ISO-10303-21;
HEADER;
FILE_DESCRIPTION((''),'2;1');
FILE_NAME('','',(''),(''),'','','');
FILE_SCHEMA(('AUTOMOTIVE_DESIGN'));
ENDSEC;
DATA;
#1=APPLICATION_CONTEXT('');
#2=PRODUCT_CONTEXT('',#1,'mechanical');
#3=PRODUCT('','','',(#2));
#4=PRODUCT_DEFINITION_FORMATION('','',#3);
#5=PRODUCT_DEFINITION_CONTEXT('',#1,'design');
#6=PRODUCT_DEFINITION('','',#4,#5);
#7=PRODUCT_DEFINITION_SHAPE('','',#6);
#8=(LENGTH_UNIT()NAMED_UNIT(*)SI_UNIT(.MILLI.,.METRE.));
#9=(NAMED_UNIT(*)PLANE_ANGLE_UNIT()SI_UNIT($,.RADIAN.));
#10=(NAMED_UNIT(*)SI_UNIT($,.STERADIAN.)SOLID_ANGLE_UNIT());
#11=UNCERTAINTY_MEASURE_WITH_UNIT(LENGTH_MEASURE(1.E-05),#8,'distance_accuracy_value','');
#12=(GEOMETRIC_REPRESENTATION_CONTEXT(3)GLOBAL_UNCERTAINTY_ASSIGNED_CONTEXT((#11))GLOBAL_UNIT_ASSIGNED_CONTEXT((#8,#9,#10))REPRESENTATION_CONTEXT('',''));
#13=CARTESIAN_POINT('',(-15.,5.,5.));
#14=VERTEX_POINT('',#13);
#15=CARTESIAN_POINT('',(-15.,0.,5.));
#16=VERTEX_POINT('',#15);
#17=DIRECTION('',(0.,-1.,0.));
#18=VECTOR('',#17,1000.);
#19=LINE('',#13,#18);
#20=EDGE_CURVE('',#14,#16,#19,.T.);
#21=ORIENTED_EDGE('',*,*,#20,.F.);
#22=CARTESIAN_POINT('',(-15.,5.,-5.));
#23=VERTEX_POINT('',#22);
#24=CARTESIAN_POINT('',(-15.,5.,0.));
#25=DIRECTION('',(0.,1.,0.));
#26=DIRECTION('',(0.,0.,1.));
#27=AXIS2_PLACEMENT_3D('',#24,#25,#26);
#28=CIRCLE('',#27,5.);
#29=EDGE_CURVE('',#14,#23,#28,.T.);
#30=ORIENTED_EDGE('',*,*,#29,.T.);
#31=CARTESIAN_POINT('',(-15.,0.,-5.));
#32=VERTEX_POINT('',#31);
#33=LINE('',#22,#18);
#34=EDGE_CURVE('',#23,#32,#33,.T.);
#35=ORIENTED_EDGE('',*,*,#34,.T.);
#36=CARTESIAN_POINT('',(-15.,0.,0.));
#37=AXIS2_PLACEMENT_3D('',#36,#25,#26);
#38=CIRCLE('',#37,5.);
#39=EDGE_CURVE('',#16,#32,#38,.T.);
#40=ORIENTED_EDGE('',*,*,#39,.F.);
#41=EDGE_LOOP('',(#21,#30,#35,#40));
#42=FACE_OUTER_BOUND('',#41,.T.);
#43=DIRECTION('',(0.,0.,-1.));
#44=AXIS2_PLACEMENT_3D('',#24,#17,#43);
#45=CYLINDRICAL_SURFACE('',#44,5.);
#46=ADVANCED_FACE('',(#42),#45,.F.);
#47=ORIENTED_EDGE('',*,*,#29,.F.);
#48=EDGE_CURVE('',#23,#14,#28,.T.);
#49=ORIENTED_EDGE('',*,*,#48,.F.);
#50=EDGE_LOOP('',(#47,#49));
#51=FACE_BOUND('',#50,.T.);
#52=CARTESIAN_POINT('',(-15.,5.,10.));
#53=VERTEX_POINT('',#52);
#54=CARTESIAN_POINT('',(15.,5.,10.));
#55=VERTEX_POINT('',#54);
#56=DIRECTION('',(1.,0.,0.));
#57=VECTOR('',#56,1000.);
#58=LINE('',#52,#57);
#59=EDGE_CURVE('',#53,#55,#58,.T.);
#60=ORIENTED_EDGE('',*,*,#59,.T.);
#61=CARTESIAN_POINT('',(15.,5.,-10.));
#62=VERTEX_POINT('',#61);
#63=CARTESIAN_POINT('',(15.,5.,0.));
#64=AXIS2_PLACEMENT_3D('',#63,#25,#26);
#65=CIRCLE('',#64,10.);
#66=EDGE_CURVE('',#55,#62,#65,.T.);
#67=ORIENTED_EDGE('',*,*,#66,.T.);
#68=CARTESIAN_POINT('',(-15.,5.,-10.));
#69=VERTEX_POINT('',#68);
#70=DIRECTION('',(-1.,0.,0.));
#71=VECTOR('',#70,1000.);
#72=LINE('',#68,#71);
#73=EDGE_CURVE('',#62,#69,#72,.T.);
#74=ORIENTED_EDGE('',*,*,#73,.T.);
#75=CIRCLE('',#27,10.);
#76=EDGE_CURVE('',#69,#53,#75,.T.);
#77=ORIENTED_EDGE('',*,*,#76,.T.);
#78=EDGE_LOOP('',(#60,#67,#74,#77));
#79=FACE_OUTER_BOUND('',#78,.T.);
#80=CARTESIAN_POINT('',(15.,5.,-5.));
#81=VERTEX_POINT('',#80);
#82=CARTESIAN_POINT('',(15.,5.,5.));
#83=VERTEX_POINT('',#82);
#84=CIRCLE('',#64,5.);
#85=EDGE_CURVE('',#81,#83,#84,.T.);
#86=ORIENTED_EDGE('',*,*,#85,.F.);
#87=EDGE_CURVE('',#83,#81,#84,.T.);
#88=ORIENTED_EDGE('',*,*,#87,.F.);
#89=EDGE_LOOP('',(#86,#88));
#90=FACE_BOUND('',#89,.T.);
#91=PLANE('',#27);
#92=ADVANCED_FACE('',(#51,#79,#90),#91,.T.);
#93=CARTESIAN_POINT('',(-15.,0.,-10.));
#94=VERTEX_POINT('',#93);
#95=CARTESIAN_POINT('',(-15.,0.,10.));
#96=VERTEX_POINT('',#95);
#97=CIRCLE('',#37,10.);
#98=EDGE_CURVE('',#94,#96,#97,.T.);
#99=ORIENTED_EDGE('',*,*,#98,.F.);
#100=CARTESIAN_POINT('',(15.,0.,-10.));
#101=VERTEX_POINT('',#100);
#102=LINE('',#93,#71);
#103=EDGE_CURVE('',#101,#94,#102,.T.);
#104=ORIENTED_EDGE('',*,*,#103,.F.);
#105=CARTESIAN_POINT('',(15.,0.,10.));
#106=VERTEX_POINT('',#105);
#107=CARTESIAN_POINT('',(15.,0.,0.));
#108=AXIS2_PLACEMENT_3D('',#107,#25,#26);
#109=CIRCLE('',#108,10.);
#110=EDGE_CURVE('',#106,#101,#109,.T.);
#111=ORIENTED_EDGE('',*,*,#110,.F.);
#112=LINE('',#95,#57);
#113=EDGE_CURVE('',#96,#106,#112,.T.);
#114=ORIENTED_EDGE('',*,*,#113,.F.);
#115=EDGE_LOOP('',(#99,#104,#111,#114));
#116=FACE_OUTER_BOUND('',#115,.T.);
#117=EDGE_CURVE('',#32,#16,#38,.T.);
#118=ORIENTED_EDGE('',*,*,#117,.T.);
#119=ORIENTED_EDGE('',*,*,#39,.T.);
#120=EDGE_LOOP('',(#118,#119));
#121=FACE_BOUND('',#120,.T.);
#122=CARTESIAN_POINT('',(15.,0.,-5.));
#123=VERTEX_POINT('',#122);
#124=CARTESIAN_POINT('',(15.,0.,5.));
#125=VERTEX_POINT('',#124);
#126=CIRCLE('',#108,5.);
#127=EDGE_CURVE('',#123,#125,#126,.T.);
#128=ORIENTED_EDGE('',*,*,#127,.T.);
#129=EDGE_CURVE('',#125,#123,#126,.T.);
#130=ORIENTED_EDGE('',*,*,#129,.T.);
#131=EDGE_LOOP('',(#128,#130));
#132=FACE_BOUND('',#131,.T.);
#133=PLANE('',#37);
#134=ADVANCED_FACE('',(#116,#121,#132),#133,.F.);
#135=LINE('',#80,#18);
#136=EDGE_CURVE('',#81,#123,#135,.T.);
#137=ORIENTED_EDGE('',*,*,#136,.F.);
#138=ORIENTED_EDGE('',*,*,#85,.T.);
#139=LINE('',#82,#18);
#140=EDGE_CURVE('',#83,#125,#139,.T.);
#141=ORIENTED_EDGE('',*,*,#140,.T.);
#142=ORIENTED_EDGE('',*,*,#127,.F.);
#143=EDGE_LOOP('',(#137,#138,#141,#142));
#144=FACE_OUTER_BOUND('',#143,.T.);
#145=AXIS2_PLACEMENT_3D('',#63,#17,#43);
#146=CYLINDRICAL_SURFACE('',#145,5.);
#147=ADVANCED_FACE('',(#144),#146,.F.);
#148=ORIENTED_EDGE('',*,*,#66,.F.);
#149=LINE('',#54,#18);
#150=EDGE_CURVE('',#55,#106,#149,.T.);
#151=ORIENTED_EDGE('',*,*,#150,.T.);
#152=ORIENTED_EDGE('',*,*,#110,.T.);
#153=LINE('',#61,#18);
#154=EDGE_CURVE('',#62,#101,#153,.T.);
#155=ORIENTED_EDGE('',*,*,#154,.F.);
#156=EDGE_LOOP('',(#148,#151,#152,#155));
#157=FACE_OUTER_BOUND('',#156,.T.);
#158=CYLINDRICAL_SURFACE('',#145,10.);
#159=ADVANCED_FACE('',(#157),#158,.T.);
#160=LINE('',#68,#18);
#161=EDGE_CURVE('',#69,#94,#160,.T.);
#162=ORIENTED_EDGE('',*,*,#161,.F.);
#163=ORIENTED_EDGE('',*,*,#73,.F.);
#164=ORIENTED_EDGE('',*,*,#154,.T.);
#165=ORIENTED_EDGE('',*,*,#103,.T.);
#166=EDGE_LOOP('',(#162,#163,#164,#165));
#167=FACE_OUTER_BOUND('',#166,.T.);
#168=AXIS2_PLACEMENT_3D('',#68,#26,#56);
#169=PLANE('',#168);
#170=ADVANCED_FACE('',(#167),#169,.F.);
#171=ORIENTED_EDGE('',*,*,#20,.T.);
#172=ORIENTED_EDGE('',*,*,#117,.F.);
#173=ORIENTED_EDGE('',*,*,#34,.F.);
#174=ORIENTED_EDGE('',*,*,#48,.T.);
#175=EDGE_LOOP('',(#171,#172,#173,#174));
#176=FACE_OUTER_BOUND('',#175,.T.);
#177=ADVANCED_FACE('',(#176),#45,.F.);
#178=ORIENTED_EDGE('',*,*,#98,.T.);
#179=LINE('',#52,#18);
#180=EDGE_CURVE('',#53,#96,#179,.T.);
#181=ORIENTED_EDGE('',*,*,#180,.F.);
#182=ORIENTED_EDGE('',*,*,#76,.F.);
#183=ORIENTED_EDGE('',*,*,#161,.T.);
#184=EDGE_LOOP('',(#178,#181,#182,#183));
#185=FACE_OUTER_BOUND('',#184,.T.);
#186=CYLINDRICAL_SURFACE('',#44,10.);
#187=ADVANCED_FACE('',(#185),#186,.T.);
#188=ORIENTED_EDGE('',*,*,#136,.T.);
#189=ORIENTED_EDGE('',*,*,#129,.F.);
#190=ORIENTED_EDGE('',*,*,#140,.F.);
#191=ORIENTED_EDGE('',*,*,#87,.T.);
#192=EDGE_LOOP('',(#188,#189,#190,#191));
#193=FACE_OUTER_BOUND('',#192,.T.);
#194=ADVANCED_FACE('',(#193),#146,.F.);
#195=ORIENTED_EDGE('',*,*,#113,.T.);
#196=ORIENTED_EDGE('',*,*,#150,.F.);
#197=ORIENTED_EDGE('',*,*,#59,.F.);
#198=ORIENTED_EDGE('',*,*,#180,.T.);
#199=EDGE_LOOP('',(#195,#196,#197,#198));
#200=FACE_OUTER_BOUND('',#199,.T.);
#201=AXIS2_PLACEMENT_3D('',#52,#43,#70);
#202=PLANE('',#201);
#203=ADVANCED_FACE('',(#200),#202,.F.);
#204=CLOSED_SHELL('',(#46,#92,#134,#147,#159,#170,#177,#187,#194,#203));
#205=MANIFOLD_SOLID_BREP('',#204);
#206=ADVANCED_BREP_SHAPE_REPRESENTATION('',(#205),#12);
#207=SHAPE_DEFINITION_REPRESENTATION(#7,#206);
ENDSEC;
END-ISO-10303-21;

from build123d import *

# Parameters (mm, degrees)
LINK_PROFILE_R       = 5
LINK_PLATE_5MM_DEPTH = 5


with BuildPart() as part:
    # Link Profile → Link Plate 5mm (new body)
    with BuildSketch(Plane(origin=(0, 0, 0), x_dir=(1, 0, 0), z_dir=(0, 1, 0))):
        with BuildLine():
            Line((-15, 10), (15, 10))
            ThreePointArc((15, 10), (25, 0), (15, -10))
            Line((15, -10), (-15, -10))
            ThreePointArc((-15, -10), (-25, 0), (-15, 10))
        make_face()
        with Locations(Location((-15, 0, 0), (0, 0, 270))):
            Circle(LINK_PROFILE_R, mode=Mode.SUBTRACT)
        with Locations(Location((15, 0, 0), (0, 0, 270))):
            Circle(LINK_PROFILE_R, mode=Mode.SUBTRACT)
    extrude(amount=LINK_PLATE_5MM_DEPTH)


solid = part.part
